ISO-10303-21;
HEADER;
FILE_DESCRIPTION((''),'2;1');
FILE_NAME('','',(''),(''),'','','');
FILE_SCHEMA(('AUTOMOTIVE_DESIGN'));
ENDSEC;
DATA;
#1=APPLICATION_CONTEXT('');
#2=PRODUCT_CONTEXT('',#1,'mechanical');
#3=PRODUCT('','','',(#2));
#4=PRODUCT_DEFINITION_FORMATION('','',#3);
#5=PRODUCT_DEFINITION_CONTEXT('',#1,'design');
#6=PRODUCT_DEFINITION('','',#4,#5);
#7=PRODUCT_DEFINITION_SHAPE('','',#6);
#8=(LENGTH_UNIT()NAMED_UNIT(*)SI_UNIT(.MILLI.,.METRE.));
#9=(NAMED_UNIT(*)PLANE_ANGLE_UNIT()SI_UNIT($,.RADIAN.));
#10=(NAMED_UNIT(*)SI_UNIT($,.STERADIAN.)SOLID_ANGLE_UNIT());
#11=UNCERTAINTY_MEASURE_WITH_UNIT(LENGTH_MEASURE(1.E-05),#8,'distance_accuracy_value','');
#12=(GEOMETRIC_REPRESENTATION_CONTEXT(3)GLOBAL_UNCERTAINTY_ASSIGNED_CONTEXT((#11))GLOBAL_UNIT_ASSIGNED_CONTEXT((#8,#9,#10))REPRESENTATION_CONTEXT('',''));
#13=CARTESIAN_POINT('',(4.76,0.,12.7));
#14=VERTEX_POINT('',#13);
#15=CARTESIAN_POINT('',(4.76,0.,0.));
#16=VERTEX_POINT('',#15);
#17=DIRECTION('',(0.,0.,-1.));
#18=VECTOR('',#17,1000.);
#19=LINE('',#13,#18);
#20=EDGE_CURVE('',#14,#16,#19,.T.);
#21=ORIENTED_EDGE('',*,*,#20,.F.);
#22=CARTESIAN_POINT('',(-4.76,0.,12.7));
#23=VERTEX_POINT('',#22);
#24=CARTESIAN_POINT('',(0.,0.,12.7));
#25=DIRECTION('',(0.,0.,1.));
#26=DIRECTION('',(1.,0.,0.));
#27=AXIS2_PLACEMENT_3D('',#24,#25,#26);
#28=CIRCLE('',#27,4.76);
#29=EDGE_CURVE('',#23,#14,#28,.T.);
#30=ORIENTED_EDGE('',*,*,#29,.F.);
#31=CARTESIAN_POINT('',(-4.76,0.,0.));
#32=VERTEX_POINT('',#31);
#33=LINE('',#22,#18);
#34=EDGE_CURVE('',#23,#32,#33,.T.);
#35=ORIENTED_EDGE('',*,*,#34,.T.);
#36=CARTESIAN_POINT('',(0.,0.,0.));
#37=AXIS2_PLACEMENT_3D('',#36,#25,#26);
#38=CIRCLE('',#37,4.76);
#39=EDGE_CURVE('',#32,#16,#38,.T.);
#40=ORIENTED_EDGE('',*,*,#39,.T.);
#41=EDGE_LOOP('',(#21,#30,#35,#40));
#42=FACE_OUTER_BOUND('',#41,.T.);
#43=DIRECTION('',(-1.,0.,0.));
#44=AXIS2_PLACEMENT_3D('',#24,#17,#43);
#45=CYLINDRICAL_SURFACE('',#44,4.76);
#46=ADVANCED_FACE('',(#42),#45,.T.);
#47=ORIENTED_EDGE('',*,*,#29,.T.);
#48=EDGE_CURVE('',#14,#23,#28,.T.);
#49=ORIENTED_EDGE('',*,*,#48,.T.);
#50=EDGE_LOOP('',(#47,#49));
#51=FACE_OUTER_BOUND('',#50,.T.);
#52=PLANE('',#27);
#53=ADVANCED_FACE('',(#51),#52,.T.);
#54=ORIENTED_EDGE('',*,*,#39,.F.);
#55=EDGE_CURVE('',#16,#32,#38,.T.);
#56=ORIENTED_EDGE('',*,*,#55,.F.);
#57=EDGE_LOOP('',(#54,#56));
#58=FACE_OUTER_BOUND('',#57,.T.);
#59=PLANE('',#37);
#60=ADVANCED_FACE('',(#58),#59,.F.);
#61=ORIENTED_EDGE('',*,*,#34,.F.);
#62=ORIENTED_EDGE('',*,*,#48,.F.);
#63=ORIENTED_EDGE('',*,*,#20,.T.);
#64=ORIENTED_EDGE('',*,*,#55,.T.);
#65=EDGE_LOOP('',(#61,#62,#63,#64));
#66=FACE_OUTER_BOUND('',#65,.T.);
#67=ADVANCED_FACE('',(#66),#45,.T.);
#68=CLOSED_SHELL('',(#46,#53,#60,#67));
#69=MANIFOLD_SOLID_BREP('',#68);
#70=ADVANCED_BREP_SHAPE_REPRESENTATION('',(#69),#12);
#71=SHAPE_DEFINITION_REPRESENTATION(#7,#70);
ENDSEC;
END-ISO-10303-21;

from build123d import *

# Parameters (mm, degrees)
PIN_PROFILE_9_52_R          = 4.76
PIN_BODY_EXTRUDE_12_7_DEPTH = 12.7


with BuildPart() as part:
    # Pin Profile Ø9.52 → Pin Body Extrude 12.7 (new body)
    with BuildSketch(Plane.XY):
        Circle(PIN_PROFILE_9_52_R)
    extrude(amount=PIN_BODY_EXTRUDE_12_7_DEPTH)


solid = part.part
